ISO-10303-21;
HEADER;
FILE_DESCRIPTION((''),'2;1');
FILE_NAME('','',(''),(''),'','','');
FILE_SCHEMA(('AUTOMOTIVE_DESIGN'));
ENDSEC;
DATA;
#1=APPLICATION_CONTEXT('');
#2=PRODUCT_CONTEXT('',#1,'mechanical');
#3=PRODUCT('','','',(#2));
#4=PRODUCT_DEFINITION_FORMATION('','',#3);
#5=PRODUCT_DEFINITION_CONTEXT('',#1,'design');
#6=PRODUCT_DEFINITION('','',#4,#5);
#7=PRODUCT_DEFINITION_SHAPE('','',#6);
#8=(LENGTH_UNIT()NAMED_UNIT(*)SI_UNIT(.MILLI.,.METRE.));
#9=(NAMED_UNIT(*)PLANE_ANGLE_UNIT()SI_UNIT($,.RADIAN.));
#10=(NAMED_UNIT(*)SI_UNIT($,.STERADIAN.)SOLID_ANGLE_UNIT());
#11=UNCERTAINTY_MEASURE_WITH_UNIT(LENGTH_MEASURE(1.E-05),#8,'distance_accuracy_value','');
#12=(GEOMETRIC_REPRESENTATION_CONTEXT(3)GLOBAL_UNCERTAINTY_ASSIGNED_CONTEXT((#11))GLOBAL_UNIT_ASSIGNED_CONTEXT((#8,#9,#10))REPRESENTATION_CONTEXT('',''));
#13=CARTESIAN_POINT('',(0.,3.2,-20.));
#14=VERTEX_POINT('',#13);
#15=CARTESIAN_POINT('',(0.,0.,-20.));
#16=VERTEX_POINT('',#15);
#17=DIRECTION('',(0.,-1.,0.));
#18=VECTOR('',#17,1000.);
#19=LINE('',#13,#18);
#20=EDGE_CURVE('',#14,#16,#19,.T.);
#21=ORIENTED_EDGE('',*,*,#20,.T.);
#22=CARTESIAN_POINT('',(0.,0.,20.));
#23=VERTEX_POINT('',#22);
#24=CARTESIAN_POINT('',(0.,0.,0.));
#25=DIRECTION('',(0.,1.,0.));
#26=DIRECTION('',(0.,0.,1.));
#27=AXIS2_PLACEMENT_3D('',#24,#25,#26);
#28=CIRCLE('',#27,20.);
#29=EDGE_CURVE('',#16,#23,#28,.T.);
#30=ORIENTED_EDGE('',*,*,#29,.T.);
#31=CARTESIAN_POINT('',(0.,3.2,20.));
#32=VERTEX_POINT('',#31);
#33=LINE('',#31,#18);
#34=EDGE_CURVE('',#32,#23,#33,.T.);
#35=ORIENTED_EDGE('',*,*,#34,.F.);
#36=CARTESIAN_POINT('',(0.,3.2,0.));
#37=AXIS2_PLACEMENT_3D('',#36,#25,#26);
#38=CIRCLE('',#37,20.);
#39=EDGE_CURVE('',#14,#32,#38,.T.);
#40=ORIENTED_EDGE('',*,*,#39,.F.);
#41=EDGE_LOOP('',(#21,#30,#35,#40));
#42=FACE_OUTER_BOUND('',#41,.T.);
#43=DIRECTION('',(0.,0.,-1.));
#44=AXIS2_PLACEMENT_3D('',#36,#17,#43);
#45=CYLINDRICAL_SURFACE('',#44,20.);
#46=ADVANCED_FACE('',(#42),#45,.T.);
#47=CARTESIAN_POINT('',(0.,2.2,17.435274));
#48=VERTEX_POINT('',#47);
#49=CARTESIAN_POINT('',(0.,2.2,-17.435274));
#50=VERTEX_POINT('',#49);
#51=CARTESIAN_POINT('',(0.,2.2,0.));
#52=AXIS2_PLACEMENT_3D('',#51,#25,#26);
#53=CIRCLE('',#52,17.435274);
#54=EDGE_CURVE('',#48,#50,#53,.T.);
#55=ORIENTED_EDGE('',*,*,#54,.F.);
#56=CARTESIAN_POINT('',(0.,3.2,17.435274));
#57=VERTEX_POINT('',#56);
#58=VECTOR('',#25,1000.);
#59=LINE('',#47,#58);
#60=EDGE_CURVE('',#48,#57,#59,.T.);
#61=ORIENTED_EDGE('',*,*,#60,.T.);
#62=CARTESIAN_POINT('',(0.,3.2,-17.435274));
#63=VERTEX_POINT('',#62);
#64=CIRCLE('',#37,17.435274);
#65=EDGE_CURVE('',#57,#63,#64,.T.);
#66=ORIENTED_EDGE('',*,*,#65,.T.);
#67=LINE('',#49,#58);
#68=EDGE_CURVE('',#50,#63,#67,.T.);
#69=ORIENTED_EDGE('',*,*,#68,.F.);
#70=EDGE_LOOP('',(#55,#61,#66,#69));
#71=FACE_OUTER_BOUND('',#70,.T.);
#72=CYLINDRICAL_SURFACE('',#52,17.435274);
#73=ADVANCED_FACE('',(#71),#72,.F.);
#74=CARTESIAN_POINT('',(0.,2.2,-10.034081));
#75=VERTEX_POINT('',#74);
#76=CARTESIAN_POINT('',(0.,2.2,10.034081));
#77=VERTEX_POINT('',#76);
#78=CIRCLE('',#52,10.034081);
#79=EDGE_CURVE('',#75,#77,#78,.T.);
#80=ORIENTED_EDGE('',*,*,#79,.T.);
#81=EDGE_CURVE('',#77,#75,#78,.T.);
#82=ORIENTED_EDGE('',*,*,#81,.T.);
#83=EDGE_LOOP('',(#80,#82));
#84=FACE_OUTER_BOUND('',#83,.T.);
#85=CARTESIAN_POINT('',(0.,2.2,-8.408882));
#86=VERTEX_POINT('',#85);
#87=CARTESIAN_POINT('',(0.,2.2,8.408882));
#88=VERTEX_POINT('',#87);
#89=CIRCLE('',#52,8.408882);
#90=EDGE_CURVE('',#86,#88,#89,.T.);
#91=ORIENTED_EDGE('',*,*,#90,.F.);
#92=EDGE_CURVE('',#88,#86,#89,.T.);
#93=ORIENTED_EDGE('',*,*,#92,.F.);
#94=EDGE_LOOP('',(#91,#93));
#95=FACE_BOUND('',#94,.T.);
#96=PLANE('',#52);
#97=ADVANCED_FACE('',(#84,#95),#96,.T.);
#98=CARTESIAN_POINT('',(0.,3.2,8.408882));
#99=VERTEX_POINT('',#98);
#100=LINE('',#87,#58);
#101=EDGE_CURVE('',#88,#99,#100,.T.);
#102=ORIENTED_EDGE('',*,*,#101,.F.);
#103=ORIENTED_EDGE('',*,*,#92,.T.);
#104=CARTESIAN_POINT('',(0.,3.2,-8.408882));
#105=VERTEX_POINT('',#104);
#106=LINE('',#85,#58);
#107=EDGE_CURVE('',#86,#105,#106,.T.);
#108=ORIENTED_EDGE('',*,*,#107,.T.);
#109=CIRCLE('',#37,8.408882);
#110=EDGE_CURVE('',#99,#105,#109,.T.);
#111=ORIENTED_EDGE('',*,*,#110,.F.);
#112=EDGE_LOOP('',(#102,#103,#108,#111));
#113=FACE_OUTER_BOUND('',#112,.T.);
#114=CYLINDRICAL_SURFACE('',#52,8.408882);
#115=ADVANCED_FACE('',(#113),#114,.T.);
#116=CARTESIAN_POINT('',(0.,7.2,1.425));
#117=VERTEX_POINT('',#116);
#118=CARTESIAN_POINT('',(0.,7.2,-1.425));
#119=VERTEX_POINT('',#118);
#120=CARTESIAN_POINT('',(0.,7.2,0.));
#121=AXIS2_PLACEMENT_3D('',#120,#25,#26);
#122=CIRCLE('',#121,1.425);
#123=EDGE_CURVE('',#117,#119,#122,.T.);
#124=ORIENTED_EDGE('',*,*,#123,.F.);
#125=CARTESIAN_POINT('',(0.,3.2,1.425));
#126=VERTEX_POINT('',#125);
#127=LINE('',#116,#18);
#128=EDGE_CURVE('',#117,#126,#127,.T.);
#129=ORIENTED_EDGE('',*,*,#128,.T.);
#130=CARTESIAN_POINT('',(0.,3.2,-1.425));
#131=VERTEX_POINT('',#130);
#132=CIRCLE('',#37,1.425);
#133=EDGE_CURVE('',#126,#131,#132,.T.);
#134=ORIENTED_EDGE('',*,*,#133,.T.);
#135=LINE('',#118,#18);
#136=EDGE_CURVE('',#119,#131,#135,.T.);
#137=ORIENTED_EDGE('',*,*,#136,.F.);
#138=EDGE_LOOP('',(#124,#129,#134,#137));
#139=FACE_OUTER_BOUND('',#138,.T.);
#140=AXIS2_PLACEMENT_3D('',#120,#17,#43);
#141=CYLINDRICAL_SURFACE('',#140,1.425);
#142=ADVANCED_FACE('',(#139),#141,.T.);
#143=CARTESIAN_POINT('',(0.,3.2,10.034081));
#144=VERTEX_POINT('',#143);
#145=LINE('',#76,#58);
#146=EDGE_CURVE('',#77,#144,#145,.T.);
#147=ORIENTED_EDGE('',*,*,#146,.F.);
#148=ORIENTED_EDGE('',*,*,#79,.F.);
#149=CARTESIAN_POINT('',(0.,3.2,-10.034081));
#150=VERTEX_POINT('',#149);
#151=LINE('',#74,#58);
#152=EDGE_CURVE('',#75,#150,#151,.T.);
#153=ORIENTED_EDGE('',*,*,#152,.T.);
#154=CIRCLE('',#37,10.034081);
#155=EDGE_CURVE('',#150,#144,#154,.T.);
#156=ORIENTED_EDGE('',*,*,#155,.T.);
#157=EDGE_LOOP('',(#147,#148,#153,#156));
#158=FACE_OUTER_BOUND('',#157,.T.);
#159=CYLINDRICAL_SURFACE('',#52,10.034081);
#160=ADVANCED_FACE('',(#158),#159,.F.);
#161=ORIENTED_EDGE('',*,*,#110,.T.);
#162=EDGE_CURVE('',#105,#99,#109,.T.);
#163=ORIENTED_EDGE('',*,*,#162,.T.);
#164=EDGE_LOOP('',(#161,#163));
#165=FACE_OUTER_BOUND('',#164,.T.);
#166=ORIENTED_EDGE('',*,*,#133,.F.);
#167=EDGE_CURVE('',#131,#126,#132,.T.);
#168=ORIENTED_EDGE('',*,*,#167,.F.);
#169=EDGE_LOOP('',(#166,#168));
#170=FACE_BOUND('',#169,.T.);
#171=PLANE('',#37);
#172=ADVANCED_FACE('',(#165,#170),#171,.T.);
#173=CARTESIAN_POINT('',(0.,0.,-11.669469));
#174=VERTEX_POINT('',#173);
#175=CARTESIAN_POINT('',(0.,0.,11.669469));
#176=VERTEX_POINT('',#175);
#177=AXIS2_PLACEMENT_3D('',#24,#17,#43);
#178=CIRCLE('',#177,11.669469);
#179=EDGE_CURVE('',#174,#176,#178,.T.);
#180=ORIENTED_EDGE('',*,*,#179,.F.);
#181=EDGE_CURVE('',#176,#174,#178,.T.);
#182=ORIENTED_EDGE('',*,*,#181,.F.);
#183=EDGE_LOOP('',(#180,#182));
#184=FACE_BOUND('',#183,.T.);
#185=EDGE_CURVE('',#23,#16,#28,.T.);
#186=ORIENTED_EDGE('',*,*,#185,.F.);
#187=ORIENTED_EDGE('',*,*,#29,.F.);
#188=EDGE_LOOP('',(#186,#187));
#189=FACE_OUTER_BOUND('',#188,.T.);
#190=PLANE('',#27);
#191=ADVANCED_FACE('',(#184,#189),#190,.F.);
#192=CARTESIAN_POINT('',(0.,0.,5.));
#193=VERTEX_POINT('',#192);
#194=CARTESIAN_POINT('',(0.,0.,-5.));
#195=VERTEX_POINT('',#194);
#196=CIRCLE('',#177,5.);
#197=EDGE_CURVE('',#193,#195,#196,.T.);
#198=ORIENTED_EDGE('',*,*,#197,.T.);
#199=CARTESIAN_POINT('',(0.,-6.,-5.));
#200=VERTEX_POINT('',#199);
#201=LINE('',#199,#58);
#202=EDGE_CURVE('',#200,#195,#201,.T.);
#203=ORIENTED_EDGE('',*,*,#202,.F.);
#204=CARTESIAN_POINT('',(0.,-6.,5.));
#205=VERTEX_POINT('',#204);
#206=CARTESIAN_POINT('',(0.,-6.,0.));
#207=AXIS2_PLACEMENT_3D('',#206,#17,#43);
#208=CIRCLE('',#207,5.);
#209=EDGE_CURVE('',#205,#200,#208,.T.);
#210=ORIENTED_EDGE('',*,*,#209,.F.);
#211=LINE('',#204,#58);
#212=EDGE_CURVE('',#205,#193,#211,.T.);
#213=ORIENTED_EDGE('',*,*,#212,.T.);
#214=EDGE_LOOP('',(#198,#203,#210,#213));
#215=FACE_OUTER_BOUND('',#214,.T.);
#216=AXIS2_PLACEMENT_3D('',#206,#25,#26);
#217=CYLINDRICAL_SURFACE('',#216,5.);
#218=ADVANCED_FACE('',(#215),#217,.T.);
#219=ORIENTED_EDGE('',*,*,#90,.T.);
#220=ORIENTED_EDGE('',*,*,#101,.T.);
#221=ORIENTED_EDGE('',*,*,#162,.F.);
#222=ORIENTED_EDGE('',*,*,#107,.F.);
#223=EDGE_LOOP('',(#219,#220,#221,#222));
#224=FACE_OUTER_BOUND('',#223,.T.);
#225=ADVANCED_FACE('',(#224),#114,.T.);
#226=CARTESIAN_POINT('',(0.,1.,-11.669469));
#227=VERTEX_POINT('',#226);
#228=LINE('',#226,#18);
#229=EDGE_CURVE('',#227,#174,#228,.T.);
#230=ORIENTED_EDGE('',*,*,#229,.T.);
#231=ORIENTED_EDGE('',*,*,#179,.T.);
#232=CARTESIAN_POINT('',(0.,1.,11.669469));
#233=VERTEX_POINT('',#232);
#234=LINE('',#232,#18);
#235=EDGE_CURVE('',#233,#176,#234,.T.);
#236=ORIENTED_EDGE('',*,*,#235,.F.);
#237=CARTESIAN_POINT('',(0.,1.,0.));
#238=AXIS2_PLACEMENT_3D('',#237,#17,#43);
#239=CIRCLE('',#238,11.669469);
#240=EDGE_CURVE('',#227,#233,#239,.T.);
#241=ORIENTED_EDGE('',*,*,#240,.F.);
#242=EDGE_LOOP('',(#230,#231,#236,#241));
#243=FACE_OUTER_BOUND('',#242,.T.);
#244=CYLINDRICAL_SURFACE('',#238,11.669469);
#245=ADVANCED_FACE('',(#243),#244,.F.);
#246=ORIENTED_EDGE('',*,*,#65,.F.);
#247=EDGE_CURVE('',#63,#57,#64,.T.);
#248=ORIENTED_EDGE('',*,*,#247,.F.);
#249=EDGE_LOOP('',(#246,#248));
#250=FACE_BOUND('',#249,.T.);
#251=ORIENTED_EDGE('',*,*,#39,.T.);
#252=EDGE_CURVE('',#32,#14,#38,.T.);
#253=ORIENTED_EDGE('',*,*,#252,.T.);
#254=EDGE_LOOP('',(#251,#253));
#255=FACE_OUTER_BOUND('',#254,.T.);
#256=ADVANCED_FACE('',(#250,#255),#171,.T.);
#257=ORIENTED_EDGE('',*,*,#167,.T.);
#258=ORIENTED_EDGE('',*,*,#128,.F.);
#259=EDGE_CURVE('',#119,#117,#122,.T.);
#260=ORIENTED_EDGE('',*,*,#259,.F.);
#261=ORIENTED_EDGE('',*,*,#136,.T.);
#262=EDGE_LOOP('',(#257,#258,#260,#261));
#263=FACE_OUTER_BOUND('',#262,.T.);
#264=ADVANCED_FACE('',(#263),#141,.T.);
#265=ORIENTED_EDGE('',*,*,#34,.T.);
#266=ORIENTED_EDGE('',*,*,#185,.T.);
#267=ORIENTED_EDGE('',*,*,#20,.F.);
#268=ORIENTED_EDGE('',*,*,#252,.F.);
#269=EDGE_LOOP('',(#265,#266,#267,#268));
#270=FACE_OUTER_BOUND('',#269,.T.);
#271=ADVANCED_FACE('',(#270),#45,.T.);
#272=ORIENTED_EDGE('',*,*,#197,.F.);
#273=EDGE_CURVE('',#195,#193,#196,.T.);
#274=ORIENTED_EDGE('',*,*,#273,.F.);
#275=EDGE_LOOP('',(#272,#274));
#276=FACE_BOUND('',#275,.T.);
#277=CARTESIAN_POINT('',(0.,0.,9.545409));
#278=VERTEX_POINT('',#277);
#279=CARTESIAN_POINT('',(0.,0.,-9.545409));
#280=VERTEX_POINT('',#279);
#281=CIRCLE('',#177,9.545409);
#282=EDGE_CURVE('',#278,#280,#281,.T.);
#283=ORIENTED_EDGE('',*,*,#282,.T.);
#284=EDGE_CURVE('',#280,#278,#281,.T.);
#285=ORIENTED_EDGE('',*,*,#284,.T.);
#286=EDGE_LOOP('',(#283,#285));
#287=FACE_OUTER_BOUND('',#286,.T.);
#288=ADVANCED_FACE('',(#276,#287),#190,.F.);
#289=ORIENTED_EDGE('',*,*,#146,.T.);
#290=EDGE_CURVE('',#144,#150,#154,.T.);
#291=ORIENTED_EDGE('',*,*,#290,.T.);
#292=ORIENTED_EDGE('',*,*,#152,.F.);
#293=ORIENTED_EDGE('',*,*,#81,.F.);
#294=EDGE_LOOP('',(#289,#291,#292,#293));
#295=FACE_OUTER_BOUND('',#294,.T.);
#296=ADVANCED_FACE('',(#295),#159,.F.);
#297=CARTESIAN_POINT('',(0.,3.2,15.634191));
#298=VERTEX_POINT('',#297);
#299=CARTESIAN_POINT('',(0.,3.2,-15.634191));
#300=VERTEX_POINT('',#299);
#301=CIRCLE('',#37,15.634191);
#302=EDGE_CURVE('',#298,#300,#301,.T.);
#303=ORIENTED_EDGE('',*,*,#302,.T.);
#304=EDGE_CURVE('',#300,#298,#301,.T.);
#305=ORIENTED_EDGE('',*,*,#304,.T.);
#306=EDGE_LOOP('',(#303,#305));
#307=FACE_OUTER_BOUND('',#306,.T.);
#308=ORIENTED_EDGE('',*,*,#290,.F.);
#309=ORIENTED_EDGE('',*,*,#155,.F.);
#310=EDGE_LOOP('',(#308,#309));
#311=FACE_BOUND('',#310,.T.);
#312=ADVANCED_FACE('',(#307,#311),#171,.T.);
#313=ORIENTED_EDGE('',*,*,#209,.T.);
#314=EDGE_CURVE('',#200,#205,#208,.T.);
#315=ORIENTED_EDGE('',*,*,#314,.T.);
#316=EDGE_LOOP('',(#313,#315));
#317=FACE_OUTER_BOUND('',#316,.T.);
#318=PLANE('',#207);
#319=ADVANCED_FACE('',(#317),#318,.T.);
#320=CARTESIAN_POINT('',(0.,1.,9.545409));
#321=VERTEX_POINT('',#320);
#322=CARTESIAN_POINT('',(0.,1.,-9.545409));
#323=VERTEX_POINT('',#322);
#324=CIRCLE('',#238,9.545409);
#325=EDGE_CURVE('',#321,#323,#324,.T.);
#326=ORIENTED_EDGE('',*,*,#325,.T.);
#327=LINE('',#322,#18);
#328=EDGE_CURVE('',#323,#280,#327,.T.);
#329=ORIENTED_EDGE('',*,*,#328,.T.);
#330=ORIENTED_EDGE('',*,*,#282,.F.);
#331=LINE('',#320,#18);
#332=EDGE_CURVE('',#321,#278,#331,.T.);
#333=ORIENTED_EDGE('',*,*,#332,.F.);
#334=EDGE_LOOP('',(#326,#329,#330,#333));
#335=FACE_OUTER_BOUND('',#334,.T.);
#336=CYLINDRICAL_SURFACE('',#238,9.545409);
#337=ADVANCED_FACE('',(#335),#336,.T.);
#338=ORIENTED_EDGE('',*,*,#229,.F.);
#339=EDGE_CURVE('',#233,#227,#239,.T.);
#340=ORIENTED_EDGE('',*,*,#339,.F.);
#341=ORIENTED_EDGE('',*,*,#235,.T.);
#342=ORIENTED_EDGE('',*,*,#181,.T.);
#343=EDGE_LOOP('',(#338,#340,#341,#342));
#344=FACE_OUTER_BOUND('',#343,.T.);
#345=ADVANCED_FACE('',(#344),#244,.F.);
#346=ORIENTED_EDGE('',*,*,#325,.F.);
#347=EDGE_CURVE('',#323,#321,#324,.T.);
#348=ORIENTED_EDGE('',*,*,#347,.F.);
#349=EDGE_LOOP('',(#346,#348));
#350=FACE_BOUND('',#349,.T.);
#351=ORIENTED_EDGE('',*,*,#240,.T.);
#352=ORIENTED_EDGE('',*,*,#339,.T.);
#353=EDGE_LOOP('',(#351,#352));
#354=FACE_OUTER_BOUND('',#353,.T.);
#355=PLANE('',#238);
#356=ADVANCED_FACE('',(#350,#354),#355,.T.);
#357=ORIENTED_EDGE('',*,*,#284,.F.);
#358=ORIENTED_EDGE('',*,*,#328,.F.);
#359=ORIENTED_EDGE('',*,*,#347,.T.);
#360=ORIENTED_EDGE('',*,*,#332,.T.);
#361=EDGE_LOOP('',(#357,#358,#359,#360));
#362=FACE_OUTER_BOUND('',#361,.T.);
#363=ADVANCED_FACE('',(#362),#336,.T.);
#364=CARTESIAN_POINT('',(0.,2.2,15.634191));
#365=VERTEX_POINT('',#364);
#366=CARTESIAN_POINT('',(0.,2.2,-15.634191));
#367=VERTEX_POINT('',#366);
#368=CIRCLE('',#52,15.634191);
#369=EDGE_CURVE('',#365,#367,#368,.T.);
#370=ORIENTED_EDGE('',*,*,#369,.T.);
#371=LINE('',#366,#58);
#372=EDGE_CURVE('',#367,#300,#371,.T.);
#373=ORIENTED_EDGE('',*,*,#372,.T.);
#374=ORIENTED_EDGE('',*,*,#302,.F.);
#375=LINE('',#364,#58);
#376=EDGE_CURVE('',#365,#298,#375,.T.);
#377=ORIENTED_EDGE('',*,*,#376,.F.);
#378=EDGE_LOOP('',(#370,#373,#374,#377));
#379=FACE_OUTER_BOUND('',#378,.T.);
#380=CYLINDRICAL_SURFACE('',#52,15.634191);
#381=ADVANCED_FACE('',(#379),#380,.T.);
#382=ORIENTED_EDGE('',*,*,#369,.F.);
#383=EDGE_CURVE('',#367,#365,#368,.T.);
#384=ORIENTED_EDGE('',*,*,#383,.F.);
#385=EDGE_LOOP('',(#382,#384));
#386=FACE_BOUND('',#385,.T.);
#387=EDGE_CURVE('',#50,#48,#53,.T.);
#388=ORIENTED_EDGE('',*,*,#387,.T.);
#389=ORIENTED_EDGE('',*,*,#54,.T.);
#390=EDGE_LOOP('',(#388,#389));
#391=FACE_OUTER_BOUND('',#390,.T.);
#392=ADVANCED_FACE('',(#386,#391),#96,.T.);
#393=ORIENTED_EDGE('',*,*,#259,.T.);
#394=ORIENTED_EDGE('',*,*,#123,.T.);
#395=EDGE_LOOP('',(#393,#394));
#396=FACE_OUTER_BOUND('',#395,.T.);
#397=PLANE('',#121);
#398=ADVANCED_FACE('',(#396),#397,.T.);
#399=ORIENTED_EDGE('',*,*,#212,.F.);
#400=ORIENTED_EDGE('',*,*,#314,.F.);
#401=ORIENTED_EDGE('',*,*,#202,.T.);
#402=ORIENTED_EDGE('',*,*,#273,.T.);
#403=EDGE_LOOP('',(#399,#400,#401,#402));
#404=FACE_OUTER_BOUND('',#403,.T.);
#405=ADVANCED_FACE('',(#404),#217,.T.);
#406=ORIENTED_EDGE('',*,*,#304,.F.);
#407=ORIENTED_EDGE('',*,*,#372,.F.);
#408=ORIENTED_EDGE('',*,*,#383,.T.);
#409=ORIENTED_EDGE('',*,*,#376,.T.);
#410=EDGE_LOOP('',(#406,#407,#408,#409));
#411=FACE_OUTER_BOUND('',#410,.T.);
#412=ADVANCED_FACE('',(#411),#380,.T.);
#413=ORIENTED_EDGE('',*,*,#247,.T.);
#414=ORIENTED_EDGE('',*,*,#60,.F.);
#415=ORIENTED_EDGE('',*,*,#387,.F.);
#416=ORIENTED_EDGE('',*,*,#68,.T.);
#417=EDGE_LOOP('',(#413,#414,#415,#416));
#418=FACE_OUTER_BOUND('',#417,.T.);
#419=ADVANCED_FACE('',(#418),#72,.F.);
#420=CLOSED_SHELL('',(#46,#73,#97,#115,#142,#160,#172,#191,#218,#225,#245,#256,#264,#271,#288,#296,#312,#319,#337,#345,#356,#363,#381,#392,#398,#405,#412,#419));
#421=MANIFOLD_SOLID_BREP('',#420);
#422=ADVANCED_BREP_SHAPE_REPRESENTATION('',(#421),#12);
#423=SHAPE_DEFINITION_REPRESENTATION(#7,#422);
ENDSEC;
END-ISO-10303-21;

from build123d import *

# Parameters (mm, degrees)
SKETCH_1_R          = 20
EXTRUDE_1_DEPTH     = 3.2
SKETCH_2_R          = 5
EXTRUDE_2_DEPTH     = 6
SKETCH_3_R          = 11.669468733
SKETCH_3_R_2        = 9.545408708
CUT_EXTRUDE_1_DEPTH = 1
SKETCH_4_R          = 1.425
EXTRUDE_3_DEPTH     = 4
SKETCH_5_R          = 17.435273898
SKETCH_5_R_2        = 15.634190673
CUT_EXTRUDE_2_DEPTH = 1
SKETCH_6_R          = 10.034081131
SKETCH_6_R_2        = 8.408881881
CUT_EXTRUDE_3_DEPTH = 1


with BuildPart() as part:
    # 草图1 → 凸台-拉伸1 (new body)
    with BuildSketch(Plane(origin=(0, 0, 0), x_dir=(1, 0, 0), z_dir=(0, 1, 0))):
        with Locations(Location((0, 0, 0), (0, 0, 270))):
            Circle(SKETCH_1_R)
    extrude(amount=EXTRUDE_1_DEPTH)

    # 草图2 → 凸台-拉伸2 (add)
    with BuildSketch(Plane.XZ):
        with Locations(Location((0, 0, 0), (0, 0, 270))):
            Circle(SKETCH_2_R)
    extrude(amount=EXTRUDE_2_DEPTH)

    # 草图3 → 切除-拉伸1 (cut)
    with BuildSketch(Plane.XZ):
        with Locations(Location((0, 0, 0), (0, 0, 270))):
            Circle(SKETCH_3_R)
        with Locations(Location((0, 0, 0), (0, 0, 270))):
            Circle(SKETCH_3_R_2, mode=Mode.SUBTRACT)
    extrude(amount=-CUT_EXTRUDE_1_DEPTH, mode=Mode.SUBTRACT)

    # 草图4 → 凸台-拉伸3 (add)
    with BuildSketch(Plane(origin=(0, 3.2, 0), x_dir=(1, 0, 0), z_dir=(0, 1, 0))):
        with Locations(Location((0, 0, 0), (0, 0, 270))):
            Circle(SKETCH_4_R)
    extrude(amount=EXTRUDE_3_DEPTH)

    # 草图5 → 切除-拉伸2 (cut)
    with BuildSketch(Plane(origin=(0, 3.2, 0), x_dir=(1, 0, 0), z_dir=(0, 1, 0))):
        with Locations(Location((0, 0, 0), (0, 0, 270))):
            Circle(SKETCH_5_R)
        with Locations(Location((0, 0, 0), (0, 0, 270))):
            Circle(SKETCH_5_R_2, mode=Mode.SUBTRACT)
    extrude(amount=-CUT_EXTRUDE_2_DEPTH, mode=Mode.SUBTRACT)

    # 草图6 → 切除-拉伸3 (cut)
    with BuildSketch(Plane(origin=(0, 3.2, 0), x_dir=(1, 0, 0), z_dir=(0, 1, 0))):
        with Locations(Location((0, 0, 0), (0, 0, 270))):
            Circle(SKETCH_6_R)
        with Locations(Location((0, 0, 0), (0, 0, 270))):
            Circle(SKETCH_6_R_2, mode=Mode.SUBTRACT)
    extrude(amount=-CUT_EXTRUDE_3_DEPTH, mode=Mode.SUBTRACT)


solid = part.part
